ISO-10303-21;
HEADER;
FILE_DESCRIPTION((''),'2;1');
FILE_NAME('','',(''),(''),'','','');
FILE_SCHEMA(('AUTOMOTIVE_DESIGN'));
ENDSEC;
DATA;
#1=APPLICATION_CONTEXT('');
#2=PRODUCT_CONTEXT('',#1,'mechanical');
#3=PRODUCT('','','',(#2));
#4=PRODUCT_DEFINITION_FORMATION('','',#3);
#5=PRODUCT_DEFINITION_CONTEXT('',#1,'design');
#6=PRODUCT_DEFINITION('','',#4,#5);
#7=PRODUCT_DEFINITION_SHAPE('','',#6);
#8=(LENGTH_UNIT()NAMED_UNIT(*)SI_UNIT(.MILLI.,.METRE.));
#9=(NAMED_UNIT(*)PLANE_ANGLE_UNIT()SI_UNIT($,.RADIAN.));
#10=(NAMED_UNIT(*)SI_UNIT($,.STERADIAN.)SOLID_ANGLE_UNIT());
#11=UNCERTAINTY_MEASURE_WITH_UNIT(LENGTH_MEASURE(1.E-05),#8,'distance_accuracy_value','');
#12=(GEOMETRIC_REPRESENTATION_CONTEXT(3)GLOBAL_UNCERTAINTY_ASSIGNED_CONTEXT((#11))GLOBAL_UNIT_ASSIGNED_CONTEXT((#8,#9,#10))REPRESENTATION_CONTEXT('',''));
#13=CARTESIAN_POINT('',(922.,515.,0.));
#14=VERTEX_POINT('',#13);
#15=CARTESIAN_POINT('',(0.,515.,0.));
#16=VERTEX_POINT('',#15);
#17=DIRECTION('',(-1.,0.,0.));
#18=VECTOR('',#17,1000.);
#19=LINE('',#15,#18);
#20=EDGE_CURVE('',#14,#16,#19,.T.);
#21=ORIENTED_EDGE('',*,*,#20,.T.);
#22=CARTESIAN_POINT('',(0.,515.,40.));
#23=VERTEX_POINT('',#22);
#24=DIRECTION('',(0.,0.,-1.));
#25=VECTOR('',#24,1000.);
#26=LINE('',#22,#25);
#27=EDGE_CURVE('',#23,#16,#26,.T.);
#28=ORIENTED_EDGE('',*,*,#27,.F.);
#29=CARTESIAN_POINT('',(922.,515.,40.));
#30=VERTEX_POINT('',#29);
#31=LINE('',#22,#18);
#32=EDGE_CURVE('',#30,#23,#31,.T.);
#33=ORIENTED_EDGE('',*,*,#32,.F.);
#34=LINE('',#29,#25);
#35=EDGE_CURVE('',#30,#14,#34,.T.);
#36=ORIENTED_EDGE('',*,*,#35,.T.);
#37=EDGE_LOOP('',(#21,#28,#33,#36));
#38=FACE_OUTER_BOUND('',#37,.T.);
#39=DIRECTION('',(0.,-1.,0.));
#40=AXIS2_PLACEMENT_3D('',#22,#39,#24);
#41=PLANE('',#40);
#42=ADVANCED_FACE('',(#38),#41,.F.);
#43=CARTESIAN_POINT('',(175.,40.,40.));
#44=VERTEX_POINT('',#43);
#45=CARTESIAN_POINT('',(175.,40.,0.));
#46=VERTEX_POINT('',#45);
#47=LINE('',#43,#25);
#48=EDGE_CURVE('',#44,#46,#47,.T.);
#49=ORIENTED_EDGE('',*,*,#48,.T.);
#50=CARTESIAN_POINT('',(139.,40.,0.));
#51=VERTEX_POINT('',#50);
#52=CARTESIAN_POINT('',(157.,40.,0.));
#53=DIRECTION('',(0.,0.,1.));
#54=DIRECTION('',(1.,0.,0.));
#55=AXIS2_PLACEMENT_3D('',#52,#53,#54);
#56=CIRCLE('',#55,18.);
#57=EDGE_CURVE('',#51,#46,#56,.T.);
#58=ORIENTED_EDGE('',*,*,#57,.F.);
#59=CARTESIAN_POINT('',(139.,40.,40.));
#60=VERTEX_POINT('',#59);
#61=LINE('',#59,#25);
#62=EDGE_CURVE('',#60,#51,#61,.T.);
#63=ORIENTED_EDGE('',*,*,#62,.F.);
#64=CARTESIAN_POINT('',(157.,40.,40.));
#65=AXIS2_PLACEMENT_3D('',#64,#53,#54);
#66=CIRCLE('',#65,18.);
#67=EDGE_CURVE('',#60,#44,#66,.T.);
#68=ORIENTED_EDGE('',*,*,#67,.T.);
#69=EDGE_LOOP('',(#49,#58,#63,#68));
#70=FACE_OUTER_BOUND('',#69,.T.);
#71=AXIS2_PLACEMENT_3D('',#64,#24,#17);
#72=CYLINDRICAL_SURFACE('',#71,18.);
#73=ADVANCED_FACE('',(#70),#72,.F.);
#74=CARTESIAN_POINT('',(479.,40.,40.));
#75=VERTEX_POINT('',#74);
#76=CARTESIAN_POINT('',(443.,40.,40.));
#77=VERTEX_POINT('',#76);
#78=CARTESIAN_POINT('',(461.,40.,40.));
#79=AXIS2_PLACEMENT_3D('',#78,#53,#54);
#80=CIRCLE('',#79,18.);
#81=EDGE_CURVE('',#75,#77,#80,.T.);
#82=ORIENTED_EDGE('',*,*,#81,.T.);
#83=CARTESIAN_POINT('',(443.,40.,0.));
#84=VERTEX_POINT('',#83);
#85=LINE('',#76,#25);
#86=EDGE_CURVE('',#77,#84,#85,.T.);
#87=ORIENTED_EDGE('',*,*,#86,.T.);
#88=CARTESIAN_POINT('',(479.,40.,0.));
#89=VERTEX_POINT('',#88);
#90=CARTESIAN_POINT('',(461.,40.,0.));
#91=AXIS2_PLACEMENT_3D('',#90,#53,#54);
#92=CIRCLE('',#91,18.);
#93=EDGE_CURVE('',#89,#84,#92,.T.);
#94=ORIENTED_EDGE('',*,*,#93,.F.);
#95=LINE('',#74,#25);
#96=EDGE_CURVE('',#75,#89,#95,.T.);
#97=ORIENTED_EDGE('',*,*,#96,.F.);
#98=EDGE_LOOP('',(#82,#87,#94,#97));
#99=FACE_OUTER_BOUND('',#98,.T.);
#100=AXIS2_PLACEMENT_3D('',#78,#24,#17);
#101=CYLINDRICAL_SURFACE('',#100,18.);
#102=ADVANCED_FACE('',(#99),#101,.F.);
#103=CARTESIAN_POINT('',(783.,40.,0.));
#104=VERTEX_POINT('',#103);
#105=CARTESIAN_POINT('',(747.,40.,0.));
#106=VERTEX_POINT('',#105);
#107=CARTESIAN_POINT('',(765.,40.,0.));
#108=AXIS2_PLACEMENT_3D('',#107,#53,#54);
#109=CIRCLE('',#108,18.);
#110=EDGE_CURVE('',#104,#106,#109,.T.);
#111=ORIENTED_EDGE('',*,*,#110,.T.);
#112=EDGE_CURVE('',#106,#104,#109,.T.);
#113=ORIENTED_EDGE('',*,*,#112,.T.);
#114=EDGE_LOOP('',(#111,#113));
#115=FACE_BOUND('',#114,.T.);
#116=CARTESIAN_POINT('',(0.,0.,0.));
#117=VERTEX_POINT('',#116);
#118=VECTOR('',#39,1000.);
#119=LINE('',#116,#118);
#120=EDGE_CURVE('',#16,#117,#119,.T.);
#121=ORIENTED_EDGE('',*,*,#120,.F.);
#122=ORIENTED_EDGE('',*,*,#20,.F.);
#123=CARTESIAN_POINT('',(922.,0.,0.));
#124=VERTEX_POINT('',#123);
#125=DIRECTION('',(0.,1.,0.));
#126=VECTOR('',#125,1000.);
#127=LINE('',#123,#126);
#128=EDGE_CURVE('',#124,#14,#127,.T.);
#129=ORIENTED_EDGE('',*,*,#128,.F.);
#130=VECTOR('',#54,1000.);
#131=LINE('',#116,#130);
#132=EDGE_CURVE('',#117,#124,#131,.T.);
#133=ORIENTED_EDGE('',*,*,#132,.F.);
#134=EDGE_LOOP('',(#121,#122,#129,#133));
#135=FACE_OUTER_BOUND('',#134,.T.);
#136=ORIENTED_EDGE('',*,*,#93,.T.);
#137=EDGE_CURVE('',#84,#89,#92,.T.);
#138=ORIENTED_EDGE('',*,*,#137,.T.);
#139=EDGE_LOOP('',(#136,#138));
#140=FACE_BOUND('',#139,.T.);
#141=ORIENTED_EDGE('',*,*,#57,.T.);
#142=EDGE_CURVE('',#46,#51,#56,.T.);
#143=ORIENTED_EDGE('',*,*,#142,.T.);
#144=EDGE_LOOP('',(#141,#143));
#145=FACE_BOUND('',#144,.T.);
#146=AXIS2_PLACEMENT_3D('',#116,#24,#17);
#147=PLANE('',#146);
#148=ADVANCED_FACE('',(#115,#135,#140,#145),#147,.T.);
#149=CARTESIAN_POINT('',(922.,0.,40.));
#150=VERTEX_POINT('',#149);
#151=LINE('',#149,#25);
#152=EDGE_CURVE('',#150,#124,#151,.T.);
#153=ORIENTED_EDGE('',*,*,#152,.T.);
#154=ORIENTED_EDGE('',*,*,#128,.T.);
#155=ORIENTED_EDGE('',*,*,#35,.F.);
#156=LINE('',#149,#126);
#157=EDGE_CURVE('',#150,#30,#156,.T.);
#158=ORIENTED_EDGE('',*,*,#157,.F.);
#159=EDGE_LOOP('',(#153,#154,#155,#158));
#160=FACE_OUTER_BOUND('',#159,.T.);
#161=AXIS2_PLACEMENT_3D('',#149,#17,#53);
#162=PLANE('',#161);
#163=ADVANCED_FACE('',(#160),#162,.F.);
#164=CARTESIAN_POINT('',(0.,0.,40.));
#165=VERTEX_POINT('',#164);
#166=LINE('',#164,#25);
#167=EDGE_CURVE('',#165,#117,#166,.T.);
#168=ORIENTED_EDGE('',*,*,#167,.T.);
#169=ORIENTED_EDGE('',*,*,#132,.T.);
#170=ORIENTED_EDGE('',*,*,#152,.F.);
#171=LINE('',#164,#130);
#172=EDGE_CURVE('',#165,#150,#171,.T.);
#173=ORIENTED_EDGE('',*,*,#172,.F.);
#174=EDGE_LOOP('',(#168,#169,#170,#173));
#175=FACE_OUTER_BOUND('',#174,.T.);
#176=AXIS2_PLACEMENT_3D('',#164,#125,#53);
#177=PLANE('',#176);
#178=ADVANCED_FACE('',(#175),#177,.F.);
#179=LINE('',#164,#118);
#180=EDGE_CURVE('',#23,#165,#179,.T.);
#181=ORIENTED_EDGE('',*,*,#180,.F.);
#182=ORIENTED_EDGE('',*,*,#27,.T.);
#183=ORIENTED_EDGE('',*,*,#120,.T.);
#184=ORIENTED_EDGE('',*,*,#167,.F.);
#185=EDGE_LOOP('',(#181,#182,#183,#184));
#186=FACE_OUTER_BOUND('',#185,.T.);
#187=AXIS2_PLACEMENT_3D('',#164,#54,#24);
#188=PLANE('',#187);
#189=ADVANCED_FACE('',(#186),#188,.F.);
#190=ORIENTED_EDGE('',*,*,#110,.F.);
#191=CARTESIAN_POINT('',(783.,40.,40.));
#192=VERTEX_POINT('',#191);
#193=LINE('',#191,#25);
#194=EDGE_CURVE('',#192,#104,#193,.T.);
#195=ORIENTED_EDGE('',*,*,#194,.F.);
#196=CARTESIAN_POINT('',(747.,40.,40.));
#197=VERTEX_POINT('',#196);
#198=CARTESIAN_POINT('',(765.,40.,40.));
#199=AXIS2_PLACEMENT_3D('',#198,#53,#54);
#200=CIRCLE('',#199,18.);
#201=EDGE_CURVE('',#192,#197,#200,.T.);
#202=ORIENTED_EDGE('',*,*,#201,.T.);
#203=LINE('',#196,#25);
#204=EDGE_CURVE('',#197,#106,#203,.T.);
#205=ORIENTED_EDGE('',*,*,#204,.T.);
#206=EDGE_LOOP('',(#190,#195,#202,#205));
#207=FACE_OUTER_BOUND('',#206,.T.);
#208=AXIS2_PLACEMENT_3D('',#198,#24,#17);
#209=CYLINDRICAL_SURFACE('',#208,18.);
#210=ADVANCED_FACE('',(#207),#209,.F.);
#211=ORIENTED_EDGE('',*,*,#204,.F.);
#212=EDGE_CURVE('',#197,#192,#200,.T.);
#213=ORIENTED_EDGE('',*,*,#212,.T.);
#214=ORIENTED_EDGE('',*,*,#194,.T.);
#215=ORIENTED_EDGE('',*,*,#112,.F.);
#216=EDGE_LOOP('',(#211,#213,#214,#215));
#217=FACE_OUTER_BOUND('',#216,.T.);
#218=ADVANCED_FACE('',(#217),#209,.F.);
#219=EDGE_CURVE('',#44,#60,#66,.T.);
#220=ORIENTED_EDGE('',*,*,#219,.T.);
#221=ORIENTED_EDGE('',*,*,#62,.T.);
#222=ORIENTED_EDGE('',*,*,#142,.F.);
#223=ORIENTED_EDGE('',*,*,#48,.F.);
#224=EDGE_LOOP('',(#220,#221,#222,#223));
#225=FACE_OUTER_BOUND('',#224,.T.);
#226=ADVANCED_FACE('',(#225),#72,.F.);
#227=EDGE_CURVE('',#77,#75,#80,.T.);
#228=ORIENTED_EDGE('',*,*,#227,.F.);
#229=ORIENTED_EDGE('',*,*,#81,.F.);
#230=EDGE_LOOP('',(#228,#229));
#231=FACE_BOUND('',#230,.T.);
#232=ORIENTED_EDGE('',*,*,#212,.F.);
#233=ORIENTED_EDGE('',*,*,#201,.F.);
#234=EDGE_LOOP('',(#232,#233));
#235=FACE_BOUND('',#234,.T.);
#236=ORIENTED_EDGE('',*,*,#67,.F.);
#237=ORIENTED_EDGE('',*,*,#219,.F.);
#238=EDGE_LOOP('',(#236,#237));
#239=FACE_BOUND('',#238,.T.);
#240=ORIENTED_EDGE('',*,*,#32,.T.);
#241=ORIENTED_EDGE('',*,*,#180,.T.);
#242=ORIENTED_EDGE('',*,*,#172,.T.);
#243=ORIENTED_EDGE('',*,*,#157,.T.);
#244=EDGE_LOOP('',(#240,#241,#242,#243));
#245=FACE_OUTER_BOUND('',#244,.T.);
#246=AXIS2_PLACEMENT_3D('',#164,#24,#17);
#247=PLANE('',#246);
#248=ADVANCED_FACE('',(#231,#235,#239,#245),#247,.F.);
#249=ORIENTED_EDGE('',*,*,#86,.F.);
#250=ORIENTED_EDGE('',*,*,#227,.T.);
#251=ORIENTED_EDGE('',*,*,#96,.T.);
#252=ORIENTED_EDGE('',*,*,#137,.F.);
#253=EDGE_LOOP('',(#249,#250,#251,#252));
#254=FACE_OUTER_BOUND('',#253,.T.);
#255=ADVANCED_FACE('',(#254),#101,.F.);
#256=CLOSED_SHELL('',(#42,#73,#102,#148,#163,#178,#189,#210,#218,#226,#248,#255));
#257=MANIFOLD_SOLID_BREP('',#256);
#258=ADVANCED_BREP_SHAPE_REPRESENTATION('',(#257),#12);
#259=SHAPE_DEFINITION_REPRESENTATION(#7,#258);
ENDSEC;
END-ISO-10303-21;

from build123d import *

# Parameters (mm, degrees)
SKETCH1_W           = 922
SKETCH1_H           = 515
SKETCH1_R           = 18
BOSS_EXTRUDE1_DEPTH = 40


with BuildPart() as part:
    # Sketch1 → Boss-Extrude1 (new body)
    with BuildSketch(Plane.XY):
        with Locations((461, 257.5)):
            Rectangle(SKETCH1_W, SKETCH1_H)
        with Locations((461, 40)):
            Circle(SKETCH1_R, mode=Mode.SUBTRACT)
        with Locations((765, 40)):
            Circle(SKETCH1_R, mode=Mode.SUBTRACT)
        with Locations((157, 40)):
            Circle(SKETCH1_R, mode=Mode.SUBTRACT)
    extrude(amount=BOSS_EXTRUDE1_DEPTH)


solid = part.part
